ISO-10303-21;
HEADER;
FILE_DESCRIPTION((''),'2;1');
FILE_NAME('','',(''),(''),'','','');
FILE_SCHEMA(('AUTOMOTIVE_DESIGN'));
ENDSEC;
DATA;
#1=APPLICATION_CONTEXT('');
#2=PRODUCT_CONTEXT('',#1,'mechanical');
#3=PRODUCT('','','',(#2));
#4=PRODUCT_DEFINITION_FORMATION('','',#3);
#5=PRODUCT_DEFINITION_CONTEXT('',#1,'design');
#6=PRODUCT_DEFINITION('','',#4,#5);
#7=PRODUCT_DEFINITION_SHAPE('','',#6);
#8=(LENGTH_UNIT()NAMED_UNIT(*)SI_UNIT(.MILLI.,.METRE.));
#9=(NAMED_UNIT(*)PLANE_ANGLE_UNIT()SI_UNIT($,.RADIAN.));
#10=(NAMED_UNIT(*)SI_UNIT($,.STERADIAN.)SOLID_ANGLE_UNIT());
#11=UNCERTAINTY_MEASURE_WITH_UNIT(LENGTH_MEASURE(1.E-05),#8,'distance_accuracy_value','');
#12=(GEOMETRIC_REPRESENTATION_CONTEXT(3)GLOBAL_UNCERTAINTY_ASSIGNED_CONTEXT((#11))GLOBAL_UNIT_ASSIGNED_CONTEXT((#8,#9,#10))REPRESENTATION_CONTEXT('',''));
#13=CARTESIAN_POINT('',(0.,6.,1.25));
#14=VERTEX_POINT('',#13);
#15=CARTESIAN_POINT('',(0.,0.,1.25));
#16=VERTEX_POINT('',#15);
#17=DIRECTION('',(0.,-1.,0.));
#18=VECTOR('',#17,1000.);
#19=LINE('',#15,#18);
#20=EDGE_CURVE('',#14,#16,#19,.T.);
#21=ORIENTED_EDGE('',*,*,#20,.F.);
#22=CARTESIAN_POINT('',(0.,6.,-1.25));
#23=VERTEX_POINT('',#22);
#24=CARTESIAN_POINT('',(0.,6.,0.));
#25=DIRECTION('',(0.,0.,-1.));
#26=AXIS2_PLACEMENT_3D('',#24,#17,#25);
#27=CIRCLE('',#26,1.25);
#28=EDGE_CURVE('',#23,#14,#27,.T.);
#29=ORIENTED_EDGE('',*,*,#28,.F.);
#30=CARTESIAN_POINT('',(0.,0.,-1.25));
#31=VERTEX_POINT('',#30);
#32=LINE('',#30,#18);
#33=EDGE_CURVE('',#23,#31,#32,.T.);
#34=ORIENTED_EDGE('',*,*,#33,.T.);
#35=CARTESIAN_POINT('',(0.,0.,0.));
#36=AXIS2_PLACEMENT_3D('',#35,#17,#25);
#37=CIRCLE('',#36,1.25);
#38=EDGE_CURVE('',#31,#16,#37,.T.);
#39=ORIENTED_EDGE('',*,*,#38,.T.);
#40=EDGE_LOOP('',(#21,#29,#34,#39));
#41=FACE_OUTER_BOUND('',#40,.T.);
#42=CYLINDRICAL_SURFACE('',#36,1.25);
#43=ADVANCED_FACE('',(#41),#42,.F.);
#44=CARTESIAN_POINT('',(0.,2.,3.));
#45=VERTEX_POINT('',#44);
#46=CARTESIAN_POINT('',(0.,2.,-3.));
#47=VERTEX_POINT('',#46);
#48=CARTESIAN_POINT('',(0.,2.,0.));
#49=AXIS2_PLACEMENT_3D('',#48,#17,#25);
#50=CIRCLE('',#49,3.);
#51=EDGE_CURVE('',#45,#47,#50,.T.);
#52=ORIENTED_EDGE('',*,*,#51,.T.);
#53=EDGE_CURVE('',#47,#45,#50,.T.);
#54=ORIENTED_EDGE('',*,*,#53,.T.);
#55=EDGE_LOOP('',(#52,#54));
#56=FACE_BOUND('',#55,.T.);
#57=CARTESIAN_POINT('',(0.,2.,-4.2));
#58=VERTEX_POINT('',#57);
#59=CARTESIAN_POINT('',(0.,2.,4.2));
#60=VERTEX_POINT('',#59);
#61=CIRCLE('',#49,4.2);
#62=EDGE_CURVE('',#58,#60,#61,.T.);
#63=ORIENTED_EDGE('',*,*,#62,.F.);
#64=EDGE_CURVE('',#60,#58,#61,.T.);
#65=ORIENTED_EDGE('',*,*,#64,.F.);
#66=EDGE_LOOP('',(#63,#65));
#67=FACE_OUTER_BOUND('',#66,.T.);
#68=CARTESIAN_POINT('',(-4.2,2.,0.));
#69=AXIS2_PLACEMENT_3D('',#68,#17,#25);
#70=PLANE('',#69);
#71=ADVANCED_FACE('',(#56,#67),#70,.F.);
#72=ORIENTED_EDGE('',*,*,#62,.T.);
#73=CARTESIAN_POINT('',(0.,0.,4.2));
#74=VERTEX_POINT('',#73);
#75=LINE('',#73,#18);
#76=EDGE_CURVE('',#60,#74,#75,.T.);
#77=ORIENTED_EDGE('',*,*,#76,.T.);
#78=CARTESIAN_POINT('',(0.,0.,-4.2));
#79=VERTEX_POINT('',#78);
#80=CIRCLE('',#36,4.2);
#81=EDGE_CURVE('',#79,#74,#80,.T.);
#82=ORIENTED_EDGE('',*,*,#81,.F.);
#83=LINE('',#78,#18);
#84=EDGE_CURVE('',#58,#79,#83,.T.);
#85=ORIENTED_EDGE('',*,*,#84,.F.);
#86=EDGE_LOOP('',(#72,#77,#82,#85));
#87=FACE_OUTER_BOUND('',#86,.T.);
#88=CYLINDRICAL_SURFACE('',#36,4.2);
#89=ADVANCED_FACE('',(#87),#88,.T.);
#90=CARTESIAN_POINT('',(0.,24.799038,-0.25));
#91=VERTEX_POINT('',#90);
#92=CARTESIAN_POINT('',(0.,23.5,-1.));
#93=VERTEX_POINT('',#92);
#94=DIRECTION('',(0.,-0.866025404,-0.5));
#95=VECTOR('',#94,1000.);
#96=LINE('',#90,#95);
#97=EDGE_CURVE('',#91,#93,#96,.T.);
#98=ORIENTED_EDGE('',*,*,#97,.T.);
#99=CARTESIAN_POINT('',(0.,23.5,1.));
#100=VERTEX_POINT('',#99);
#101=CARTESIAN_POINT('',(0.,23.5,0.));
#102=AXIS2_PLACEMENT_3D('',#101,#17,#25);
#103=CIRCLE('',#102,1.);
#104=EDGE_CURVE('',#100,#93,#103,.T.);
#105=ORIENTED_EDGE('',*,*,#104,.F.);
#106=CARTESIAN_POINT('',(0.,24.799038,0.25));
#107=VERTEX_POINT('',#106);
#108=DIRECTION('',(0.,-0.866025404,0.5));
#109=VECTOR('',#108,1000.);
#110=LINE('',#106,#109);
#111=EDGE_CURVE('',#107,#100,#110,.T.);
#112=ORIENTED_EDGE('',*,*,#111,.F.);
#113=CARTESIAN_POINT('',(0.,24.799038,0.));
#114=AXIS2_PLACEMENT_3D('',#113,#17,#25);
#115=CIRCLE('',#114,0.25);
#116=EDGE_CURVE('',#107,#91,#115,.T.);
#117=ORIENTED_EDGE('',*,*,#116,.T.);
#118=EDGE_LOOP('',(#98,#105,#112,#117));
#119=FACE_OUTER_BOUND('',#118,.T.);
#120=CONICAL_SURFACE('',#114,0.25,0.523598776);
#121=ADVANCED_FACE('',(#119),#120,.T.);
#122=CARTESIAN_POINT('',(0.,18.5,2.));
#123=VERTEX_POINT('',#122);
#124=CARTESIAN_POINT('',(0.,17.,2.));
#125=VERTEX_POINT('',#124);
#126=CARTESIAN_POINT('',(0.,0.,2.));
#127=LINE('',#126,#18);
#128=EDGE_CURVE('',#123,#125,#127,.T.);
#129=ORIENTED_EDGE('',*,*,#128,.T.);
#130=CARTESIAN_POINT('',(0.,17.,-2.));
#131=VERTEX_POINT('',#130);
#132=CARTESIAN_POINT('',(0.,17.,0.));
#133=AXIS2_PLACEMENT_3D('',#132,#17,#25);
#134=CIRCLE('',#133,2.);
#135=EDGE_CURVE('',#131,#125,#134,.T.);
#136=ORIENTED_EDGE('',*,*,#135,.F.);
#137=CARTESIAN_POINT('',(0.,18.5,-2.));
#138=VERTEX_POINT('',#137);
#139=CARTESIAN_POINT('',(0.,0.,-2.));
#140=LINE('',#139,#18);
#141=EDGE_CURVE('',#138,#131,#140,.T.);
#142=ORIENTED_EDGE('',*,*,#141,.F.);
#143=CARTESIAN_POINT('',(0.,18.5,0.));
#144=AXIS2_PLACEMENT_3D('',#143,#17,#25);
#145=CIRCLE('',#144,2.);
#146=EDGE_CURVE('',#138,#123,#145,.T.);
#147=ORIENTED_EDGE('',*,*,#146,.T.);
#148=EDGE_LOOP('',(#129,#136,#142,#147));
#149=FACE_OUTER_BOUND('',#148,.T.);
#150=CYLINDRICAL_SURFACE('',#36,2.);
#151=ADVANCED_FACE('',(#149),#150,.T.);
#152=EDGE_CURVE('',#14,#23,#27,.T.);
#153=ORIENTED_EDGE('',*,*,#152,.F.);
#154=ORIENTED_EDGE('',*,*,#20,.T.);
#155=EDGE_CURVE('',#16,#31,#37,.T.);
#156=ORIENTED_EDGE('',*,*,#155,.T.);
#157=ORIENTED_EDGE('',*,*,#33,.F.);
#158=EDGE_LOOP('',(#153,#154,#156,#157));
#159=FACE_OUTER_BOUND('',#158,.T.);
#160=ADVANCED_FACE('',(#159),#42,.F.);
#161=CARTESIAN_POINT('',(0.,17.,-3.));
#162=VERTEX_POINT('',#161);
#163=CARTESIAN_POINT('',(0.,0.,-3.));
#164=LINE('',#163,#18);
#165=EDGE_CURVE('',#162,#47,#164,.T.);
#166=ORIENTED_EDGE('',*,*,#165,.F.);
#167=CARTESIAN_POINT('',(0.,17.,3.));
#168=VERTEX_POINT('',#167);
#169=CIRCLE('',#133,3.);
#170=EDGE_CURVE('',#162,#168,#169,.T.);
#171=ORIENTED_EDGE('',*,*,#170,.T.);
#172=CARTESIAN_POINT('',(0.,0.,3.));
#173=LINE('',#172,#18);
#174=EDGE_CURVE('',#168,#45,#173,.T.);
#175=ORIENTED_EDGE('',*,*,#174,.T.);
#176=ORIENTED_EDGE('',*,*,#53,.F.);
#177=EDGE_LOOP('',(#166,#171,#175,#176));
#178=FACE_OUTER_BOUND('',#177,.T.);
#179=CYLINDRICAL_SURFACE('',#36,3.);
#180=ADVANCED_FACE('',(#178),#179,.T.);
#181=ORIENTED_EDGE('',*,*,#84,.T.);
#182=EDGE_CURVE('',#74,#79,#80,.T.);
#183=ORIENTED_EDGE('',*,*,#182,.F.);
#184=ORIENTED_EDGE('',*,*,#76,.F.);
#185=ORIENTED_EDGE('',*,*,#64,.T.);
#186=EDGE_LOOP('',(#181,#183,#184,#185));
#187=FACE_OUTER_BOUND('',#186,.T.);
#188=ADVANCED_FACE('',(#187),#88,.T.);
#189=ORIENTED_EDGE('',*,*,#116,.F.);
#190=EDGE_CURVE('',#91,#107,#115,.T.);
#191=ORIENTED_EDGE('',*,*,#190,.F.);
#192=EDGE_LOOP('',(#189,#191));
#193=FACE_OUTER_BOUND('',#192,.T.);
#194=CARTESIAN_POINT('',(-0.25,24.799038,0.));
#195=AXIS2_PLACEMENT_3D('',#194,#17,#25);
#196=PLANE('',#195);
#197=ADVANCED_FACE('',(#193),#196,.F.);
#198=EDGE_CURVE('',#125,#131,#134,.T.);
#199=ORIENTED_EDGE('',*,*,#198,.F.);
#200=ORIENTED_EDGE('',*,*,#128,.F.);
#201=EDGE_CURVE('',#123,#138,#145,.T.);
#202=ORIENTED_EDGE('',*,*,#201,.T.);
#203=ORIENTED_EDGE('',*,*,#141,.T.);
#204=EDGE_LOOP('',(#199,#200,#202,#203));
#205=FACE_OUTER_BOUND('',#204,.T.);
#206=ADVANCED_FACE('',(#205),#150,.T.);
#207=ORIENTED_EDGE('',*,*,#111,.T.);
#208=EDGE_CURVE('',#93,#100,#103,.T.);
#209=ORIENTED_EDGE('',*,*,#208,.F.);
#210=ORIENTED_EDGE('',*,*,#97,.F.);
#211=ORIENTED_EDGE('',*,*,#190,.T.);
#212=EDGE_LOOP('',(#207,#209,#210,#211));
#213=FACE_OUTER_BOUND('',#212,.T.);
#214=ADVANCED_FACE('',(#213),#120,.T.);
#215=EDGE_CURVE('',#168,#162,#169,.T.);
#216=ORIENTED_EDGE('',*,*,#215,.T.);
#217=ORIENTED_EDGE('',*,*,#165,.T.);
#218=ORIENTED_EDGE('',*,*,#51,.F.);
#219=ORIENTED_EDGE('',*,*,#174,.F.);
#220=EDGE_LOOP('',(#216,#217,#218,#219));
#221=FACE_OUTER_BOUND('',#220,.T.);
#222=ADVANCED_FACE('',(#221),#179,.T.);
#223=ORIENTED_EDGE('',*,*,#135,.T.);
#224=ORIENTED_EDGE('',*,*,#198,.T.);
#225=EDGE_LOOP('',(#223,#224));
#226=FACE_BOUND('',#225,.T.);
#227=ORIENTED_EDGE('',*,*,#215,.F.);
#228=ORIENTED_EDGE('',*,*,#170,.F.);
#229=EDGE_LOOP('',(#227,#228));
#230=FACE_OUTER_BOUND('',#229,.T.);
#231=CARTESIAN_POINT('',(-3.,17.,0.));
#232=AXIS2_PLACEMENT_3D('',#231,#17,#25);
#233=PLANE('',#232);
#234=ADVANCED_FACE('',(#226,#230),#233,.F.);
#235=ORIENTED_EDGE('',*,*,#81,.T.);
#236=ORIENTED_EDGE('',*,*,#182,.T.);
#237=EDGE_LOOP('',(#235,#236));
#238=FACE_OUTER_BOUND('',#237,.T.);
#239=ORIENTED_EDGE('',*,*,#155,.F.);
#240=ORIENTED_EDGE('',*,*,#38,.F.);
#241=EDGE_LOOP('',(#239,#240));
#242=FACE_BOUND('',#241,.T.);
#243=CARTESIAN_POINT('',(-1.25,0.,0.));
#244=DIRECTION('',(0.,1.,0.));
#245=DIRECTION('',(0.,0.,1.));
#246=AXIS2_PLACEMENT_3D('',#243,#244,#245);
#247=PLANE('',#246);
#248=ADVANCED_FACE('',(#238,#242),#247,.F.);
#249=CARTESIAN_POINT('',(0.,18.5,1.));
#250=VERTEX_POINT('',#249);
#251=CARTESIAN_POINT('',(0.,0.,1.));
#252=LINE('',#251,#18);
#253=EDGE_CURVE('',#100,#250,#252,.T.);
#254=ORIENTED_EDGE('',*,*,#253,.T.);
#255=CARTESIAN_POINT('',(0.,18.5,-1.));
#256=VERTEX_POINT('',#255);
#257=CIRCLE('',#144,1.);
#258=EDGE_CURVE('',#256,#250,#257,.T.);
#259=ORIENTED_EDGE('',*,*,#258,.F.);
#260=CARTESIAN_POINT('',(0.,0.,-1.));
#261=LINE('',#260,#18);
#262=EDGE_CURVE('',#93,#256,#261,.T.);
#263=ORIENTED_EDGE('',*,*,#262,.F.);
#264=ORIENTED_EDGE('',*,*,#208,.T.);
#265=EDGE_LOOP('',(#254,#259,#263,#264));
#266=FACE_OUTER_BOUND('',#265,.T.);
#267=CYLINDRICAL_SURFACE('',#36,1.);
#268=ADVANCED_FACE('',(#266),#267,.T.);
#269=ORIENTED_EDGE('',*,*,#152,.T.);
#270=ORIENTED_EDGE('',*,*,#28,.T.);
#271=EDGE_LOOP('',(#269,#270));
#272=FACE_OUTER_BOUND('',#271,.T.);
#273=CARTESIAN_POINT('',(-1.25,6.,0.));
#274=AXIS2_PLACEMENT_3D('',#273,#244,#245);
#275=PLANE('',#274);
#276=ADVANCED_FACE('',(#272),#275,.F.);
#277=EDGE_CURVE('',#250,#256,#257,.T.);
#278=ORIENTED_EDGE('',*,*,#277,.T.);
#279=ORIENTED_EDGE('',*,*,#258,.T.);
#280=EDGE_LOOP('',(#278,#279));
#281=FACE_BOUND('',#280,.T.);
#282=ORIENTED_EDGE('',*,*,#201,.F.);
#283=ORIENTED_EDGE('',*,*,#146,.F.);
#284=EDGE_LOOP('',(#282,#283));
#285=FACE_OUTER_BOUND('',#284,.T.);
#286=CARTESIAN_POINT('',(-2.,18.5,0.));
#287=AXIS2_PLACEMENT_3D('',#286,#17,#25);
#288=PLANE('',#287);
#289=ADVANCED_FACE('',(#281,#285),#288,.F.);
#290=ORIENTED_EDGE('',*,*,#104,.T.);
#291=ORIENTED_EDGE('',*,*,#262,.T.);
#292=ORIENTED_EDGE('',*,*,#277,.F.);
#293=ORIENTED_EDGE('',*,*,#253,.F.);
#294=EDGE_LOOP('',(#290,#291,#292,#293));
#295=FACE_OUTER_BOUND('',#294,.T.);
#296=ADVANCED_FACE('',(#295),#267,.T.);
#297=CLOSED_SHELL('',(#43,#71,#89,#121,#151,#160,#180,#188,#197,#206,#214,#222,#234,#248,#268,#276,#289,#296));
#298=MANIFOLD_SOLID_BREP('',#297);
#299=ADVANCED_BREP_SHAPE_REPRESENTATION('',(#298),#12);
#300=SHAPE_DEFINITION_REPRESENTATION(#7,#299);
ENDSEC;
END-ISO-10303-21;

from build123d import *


with BuildPart() as part:
    # Sketch1 → Revolve1 (revolve)
    with BuildSketch(Plane.XY, mode=Mode.PRIVATE) as revolve1_sk:
        Polygon((-1.25, 0), (-4.2, 0), (-4.2, 2), (-3, 2), (-3, 17), (-2, 17), (-2, 18.5), (-1, 18.5), (-1, 23.5), (-0.25, 24.799038106), (0, 24.799038106), (0, 6), (-1.25, 6), align=None)
    revolve(revolve1_sk.sketch.rotate(Axis((0, 0, 0), (0, 1, 0)), 270), axis=Axis((0, 0, 0), (0, 1, 0)))


solid = part.part
